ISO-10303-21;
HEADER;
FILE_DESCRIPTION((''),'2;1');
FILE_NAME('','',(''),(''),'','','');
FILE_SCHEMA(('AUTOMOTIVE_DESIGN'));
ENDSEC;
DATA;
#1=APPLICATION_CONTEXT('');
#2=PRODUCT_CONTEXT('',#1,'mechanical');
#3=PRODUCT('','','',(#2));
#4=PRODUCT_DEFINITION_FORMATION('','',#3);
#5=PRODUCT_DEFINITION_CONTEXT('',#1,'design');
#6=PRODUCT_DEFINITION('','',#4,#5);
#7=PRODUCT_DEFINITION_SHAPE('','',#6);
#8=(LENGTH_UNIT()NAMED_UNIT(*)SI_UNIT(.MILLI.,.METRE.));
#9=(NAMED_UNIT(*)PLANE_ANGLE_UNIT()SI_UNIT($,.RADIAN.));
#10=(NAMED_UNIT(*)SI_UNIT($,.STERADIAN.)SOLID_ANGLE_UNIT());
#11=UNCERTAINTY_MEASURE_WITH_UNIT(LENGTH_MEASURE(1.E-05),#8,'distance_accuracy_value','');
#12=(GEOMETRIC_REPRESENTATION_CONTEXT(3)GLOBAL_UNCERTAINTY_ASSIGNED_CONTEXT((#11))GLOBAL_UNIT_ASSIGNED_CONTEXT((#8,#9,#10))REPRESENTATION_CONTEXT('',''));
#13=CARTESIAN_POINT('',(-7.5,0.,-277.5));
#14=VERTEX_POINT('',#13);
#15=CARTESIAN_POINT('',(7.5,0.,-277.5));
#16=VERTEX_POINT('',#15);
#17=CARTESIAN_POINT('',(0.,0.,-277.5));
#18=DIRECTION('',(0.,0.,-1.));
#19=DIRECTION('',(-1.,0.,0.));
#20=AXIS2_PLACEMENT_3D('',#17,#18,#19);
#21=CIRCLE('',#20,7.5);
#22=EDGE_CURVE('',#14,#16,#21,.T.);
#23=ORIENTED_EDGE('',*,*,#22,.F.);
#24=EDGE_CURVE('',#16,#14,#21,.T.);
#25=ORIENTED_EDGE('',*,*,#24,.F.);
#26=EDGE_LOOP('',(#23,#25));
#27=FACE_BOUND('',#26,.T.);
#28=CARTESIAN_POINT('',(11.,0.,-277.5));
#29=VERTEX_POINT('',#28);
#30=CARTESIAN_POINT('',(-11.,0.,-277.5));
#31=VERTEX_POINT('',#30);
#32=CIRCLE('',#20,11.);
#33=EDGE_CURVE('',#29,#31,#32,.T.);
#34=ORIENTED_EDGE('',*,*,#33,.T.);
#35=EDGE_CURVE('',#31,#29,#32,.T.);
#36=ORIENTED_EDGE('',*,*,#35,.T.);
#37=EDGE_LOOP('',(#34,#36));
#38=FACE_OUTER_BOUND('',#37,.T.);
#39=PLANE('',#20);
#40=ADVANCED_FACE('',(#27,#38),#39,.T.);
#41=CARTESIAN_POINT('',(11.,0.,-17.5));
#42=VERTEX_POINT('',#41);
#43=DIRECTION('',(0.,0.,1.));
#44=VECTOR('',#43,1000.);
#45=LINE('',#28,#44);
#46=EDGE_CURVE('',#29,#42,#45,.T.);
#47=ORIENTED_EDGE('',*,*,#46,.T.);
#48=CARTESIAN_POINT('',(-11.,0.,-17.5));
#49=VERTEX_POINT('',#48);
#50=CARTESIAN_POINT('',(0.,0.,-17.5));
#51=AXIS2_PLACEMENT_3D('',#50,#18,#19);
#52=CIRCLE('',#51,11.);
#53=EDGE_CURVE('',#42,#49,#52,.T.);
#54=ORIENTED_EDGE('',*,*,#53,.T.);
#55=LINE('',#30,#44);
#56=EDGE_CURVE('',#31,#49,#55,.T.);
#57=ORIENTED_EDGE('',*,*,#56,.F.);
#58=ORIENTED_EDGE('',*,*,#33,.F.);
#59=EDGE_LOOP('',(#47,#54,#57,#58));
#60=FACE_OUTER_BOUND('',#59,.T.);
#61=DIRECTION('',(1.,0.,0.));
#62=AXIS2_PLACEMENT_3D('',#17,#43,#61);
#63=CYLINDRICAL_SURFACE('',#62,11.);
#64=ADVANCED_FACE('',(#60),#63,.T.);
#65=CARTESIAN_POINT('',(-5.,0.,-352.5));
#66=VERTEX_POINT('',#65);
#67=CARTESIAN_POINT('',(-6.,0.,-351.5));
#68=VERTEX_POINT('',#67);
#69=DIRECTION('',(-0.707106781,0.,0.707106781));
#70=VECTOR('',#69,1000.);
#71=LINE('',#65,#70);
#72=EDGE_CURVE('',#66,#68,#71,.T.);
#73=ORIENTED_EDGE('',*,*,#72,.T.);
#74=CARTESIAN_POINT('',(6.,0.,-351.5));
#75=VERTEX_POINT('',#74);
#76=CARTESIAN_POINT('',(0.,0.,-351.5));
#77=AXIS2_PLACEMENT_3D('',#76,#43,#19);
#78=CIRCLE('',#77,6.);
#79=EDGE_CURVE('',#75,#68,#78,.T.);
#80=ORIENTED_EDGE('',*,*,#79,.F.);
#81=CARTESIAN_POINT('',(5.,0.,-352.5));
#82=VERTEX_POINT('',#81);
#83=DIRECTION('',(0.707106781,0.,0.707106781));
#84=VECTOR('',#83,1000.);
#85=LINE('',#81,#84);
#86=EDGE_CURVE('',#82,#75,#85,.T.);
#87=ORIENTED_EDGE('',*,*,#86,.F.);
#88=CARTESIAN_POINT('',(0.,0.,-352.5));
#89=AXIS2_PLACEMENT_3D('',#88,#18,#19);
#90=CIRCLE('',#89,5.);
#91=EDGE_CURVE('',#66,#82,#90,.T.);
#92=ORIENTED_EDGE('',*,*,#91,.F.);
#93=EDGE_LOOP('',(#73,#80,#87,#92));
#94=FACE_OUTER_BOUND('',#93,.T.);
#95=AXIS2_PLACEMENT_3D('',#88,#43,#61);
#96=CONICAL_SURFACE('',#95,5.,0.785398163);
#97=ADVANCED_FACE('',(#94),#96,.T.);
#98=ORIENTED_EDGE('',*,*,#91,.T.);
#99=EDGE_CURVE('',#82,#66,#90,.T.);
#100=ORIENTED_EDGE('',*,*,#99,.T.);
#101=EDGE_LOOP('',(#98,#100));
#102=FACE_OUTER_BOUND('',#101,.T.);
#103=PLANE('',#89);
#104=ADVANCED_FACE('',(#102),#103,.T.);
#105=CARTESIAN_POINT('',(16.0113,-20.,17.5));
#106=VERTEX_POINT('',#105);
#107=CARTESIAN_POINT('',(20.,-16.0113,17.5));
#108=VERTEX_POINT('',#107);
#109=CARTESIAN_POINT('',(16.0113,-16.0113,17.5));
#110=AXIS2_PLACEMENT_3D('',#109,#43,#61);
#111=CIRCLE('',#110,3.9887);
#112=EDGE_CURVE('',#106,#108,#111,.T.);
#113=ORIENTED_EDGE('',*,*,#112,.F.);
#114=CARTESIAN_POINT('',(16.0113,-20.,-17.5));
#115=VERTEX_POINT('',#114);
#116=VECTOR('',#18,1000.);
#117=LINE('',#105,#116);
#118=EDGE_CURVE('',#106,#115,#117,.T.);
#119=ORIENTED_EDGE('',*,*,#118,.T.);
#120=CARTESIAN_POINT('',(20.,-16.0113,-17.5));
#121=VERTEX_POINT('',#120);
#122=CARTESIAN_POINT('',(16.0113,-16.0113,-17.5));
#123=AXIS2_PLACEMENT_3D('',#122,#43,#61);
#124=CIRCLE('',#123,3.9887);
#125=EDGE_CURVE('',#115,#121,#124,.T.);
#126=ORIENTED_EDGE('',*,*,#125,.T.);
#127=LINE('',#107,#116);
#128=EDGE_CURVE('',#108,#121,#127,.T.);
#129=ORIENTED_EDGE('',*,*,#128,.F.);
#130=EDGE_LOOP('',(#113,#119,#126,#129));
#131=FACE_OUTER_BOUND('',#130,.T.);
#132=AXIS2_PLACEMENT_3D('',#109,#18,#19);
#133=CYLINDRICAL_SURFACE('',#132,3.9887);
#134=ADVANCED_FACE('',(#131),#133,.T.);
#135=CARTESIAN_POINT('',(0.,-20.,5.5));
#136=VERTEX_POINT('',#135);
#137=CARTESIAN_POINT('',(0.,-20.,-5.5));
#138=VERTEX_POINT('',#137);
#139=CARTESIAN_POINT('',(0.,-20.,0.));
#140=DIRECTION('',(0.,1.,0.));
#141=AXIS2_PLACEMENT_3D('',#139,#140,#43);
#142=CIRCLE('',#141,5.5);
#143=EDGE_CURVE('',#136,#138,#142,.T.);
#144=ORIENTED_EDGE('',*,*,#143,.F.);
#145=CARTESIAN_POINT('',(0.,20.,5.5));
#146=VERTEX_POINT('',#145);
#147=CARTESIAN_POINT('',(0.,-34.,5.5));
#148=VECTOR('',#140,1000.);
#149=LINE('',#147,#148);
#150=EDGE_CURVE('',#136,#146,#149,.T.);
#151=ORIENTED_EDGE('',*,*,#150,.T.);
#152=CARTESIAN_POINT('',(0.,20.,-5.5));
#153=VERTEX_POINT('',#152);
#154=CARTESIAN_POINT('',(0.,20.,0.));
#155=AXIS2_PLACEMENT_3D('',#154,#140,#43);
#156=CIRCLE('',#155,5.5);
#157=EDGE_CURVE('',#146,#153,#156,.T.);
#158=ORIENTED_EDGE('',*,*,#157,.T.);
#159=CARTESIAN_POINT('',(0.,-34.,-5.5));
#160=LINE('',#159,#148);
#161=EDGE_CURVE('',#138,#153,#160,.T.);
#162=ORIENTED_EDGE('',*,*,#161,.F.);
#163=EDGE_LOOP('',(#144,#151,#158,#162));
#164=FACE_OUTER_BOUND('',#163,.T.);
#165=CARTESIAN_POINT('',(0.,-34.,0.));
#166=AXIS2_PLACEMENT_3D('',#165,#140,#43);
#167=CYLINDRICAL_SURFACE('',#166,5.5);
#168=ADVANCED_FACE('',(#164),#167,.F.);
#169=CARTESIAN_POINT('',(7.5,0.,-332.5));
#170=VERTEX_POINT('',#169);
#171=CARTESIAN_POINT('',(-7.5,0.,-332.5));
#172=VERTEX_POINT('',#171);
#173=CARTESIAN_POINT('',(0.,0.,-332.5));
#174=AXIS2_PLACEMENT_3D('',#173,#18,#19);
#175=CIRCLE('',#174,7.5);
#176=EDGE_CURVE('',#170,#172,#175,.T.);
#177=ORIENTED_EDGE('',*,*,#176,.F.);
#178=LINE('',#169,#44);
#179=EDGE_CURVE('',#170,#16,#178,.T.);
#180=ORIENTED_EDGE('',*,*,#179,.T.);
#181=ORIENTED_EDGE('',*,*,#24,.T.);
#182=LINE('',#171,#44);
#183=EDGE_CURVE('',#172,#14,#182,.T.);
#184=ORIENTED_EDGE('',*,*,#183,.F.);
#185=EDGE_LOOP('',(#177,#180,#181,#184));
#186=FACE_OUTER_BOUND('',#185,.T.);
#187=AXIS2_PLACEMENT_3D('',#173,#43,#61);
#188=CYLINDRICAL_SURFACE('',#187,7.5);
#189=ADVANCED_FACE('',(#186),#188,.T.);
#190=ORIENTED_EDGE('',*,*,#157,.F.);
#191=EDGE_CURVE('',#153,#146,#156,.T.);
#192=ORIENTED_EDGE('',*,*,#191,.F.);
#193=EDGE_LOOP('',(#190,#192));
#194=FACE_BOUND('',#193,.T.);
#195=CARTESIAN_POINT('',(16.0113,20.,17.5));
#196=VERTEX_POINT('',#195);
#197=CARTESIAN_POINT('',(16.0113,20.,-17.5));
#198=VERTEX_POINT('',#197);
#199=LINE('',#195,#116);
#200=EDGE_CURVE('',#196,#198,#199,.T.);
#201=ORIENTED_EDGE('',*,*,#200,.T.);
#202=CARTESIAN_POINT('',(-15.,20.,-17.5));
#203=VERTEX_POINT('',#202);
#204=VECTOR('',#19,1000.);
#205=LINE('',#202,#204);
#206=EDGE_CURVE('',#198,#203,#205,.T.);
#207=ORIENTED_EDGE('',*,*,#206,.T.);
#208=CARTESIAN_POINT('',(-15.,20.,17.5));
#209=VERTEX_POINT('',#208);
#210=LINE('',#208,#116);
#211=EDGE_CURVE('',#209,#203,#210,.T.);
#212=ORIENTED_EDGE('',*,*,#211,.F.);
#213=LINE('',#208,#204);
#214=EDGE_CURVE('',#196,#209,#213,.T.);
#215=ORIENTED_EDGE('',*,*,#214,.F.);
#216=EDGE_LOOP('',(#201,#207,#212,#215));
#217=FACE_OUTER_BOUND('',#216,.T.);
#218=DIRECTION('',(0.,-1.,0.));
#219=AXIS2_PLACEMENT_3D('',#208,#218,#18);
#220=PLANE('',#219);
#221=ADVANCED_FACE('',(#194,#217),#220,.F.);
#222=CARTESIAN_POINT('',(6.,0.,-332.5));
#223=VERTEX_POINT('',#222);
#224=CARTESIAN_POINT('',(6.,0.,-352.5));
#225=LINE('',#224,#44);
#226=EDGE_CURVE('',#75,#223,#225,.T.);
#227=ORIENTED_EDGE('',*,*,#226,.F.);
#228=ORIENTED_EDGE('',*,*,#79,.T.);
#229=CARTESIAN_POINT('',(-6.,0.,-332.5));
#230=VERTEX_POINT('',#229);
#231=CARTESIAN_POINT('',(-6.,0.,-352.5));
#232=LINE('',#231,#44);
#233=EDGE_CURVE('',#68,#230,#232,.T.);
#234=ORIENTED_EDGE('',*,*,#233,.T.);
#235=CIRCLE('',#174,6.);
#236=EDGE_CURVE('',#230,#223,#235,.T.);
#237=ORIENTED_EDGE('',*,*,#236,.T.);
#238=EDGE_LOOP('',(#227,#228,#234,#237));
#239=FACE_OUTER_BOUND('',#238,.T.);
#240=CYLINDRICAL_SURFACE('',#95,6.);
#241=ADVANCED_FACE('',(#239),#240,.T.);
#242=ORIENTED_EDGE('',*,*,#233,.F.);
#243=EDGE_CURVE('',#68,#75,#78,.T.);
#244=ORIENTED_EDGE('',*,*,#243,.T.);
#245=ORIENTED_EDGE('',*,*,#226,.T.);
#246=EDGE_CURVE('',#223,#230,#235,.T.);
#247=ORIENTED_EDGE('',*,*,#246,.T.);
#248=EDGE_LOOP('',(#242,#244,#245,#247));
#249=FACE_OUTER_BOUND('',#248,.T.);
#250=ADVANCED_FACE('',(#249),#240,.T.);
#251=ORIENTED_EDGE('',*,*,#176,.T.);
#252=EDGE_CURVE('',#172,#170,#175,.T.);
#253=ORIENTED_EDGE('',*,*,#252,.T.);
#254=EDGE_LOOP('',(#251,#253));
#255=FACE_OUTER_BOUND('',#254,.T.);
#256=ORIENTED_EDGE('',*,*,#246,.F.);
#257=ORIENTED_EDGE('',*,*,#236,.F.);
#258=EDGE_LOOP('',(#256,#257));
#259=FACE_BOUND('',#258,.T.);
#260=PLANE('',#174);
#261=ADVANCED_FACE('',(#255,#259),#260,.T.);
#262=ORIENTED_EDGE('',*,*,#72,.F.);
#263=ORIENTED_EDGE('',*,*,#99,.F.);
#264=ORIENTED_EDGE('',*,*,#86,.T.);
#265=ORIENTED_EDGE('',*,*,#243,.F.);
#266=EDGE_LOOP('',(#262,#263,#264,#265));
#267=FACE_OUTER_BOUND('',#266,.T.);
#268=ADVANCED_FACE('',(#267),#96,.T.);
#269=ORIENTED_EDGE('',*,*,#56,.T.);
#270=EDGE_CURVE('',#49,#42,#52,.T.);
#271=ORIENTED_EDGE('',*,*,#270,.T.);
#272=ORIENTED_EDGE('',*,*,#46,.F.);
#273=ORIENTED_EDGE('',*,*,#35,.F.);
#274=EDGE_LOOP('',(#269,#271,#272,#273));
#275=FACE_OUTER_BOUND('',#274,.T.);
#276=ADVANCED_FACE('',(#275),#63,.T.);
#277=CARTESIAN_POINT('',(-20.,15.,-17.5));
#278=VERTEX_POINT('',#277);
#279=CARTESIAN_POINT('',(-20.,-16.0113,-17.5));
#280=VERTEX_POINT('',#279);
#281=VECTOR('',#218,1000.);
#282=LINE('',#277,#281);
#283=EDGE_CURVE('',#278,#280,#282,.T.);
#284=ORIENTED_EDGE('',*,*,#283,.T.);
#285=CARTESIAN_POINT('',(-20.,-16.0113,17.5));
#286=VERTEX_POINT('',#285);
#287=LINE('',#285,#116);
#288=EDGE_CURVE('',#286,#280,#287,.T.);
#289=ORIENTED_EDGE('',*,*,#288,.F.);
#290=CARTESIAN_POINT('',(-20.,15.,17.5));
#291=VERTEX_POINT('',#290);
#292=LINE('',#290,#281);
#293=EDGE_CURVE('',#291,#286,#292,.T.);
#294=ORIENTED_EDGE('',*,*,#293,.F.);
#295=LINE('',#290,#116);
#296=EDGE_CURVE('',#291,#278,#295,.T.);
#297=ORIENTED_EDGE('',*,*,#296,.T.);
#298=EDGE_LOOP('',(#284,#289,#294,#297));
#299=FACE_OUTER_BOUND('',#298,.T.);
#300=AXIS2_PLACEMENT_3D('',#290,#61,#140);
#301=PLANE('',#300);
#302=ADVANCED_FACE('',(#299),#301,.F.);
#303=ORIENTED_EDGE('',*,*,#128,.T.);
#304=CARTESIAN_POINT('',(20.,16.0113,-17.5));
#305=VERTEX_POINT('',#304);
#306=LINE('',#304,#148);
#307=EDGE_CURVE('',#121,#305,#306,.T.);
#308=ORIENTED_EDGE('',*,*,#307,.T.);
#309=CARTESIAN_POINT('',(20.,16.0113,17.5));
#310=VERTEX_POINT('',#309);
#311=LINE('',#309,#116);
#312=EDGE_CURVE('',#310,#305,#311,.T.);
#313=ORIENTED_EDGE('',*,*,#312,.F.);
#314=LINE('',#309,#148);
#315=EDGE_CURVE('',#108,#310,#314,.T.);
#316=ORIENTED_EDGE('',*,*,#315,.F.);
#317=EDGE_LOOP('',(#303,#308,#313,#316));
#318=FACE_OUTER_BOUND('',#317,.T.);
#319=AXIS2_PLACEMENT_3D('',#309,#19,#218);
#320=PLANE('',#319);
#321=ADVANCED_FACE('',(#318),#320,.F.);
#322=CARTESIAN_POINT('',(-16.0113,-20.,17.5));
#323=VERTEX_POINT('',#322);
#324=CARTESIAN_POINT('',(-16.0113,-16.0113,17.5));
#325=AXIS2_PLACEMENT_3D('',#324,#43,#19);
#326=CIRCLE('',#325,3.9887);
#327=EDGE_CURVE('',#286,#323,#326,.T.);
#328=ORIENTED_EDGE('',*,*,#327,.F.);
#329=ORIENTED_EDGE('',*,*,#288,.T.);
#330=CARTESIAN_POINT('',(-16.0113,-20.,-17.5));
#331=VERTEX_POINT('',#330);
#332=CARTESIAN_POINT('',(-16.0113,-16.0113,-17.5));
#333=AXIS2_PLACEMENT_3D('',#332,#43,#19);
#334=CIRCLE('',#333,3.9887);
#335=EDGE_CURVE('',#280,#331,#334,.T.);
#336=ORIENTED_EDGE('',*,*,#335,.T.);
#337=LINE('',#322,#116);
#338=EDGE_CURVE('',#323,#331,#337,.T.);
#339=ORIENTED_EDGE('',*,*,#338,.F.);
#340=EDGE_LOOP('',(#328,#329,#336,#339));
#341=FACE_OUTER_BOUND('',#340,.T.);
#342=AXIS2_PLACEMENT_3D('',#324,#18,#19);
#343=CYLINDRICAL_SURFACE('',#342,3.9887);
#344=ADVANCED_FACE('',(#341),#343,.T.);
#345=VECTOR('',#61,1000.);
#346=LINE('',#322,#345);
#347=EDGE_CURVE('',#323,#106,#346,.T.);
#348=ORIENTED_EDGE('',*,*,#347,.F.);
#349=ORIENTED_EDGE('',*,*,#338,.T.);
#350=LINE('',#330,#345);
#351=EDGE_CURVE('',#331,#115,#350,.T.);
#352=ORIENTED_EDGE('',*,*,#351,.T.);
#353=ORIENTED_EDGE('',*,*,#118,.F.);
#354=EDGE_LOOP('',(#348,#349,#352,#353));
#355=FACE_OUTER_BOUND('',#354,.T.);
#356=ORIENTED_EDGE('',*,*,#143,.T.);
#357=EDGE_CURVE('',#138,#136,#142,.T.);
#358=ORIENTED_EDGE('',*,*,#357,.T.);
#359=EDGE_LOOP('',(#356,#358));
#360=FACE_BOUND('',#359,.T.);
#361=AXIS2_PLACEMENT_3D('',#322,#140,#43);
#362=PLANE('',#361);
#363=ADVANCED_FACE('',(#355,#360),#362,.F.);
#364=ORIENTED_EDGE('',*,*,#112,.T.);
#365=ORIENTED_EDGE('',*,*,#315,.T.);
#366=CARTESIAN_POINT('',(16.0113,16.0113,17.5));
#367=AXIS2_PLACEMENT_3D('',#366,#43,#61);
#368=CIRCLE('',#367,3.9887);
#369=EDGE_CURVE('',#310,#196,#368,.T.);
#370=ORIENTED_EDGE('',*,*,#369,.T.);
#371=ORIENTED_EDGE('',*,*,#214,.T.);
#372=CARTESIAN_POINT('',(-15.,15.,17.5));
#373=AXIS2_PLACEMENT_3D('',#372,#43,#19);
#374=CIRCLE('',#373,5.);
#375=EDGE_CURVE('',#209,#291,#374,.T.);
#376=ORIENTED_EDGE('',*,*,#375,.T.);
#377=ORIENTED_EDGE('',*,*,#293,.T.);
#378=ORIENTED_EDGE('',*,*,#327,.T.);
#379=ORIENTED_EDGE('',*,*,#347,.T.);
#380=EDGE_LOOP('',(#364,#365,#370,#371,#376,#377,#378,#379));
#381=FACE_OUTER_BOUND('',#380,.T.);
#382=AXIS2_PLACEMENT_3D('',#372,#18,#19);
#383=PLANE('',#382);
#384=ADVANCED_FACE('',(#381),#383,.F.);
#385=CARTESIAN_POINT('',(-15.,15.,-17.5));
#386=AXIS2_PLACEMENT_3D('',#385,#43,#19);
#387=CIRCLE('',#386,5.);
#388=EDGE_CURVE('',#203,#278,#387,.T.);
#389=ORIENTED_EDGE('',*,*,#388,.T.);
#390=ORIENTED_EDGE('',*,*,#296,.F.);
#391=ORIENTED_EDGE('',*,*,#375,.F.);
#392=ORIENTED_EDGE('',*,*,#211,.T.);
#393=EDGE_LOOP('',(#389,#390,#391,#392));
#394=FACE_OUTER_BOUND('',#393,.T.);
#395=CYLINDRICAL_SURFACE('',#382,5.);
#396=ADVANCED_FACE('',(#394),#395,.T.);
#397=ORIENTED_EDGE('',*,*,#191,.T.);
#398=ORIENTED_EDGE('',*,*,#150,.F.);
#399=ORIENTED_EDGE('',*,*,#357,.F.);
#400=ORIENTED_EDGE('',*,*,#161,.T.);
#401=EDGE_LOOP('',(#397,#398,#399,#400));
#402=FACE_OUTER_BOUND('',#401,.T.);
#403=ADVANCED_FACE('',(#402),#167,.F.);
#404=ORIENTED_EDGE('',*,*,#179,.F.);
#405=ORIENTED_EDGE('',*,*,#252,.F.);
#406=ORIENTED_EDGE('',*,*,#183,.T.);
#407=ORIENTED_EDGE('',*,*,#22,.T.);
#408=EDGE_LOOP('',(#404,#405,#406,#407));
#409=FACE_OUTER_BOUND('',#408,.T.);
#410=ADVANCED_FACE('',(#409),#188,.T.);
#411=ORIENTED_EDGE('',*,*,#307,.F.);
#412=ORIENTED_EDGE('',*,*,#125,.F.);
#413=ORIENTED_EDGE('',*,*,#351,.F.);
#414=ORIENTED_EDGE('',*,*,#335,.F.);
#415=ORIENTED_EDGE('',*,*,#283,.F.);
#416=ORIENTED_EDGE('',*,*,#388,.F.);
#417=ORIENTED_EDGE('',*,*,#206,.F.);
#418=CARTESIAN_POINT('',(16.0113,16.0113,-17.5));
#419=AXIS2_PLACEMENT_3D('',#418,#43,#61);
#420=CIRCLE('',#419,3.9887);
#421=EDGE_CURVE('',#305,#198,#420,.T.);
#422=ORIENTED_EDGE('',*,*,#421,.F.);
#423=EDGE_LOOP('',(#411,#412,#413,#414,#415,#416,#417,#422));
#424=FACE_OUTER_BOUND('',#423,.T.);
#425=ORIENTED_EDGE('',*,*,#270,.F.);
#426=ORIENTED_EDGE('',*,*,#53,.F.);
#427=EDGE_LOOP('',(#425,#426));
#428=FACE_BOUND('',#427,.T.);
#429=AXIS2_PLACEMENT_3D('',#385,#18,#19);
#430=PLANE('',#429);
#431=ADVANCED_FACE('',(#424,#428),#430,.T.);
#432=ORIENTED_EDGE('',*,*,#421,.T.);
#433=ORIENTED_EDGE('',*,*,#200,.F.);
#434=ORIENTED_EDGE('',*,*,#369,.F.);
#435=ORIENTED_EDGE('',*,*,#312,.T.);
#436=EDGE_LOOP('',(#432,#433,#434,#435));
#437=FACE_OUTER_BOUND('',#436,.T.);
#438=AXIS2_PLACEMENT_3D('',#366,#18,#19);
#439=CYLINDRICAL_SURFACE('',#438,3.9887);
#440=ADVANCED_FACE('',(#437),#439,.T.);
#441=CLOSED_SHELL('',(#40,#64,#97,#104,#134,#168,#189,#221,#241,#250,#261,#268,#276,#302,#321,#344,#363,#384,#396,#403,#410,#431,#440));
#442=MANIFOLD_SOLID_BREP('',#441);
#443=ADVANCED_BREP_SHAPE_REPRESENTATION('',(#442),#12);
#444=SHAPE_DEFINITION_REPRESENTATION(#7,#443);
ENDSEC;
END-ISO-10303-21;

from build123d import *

# Parameters (mm, degrees)
BOSS_EXTRUDE2_DEPTH = 17.5
SKETCH3_R           = 5.5
CUT_EXTRUDE2_DEPTH  = 54
SKETCH4_R           = 11
BOSS_EXTRUDE3_DEPTH = 260
SKETCH5_R           = 7.5
BOSS_EXTRUDE4_DEPTH = 55
SKETCH6_R           = 6
BOSS_EXTRUDE5_DEPTH = 20
CHAMFER1_SIZE       = 1


with BuildPart() as part:
    # Sketch1 → Boss-Extrude2 (new, symmetric)
    with BuildSketch(Plane.XY):
        with BuildLine():
            Line((-15, 20), (16.011299973, 20))
            ThreePointArc((16.011299973, 20), (18.83173681, 18.83173681), (20, 16.011299973))
            Line((20, 16.011299973), (20, -16.011299973))
            ThreePointArc((20, -16.011299973), (18.83173681, -18.83173681), (16.011299973, -20))
            Line((16.011299973, -20), (-16.011299973, -20))
            ThreePointArc((-16.011299973, -20), (-18.83173681, -18.83173681), (-20, -16.011299973))
            Line((-20, -16.011299973), (-20, 15))
            ThreePointArc((-20, 15), (-18.535533906, 18.535533906), (-15, 20))
        make_face()
    extrude(amount=BOSS_EXTRUDE2_DEPTH, both=True)

    # Sketch3 → Cut-Extrude2 (cut)
    with BuildSketch(Plane(origin=(0, 20, 0), x_dir=(1, 0, 0), z_dir=(0, 1, 0))):
        with Locations(Location((0, 0, 0), (0, 0, 270))):
            Circle(SKETCH3_R)
    extrude(amount=-CUT_EXTRUDE2_DEPTH, mode=Mode.SUBTRACT)

    # Sketch4 → Boss-Extrude3 (add)
    with BuildSketch(Plane(origin=(0, 0, -17.5), x_dir=(-1, 0, 0), z_dir=(0, 0, -1))):
        Circle(SKETCH4_R)
    extrude(amount=BOSS_EXTRUDE3_DEPTH)

    # Sketch5 → Boss-Extrude4 (add)
    with BuildSketch(Plane(origin=(0, 0, -277.5), x_dir=(-1, 0, 0), z_dir=(0, 0, -1))):
        Circle(SKETCH5_R)
    extrude(amount=BOSS_EXTRUDE4_DEPTH)

    # Sketch6 → Boss-Extrude5 (add)
    with BuildSketch(Plane(origin=(0, 0, -332.5), x_dir=(-1, 0, 0), z_dir=(0, 0, -1))):
        Circle(SKETCH6_R)
    extrude(amount=BOSS_EXTRUDE5_DEPTH)

    # Chamfer1
    chamfer1_edges = [part.edges().sort_by_distance(p)[0] for p in [
        (6, 0, -352.5),
    ]]
    chamfer(chamfer1_edges, length=CHAMFER1_SIZE)


solid = part.part
